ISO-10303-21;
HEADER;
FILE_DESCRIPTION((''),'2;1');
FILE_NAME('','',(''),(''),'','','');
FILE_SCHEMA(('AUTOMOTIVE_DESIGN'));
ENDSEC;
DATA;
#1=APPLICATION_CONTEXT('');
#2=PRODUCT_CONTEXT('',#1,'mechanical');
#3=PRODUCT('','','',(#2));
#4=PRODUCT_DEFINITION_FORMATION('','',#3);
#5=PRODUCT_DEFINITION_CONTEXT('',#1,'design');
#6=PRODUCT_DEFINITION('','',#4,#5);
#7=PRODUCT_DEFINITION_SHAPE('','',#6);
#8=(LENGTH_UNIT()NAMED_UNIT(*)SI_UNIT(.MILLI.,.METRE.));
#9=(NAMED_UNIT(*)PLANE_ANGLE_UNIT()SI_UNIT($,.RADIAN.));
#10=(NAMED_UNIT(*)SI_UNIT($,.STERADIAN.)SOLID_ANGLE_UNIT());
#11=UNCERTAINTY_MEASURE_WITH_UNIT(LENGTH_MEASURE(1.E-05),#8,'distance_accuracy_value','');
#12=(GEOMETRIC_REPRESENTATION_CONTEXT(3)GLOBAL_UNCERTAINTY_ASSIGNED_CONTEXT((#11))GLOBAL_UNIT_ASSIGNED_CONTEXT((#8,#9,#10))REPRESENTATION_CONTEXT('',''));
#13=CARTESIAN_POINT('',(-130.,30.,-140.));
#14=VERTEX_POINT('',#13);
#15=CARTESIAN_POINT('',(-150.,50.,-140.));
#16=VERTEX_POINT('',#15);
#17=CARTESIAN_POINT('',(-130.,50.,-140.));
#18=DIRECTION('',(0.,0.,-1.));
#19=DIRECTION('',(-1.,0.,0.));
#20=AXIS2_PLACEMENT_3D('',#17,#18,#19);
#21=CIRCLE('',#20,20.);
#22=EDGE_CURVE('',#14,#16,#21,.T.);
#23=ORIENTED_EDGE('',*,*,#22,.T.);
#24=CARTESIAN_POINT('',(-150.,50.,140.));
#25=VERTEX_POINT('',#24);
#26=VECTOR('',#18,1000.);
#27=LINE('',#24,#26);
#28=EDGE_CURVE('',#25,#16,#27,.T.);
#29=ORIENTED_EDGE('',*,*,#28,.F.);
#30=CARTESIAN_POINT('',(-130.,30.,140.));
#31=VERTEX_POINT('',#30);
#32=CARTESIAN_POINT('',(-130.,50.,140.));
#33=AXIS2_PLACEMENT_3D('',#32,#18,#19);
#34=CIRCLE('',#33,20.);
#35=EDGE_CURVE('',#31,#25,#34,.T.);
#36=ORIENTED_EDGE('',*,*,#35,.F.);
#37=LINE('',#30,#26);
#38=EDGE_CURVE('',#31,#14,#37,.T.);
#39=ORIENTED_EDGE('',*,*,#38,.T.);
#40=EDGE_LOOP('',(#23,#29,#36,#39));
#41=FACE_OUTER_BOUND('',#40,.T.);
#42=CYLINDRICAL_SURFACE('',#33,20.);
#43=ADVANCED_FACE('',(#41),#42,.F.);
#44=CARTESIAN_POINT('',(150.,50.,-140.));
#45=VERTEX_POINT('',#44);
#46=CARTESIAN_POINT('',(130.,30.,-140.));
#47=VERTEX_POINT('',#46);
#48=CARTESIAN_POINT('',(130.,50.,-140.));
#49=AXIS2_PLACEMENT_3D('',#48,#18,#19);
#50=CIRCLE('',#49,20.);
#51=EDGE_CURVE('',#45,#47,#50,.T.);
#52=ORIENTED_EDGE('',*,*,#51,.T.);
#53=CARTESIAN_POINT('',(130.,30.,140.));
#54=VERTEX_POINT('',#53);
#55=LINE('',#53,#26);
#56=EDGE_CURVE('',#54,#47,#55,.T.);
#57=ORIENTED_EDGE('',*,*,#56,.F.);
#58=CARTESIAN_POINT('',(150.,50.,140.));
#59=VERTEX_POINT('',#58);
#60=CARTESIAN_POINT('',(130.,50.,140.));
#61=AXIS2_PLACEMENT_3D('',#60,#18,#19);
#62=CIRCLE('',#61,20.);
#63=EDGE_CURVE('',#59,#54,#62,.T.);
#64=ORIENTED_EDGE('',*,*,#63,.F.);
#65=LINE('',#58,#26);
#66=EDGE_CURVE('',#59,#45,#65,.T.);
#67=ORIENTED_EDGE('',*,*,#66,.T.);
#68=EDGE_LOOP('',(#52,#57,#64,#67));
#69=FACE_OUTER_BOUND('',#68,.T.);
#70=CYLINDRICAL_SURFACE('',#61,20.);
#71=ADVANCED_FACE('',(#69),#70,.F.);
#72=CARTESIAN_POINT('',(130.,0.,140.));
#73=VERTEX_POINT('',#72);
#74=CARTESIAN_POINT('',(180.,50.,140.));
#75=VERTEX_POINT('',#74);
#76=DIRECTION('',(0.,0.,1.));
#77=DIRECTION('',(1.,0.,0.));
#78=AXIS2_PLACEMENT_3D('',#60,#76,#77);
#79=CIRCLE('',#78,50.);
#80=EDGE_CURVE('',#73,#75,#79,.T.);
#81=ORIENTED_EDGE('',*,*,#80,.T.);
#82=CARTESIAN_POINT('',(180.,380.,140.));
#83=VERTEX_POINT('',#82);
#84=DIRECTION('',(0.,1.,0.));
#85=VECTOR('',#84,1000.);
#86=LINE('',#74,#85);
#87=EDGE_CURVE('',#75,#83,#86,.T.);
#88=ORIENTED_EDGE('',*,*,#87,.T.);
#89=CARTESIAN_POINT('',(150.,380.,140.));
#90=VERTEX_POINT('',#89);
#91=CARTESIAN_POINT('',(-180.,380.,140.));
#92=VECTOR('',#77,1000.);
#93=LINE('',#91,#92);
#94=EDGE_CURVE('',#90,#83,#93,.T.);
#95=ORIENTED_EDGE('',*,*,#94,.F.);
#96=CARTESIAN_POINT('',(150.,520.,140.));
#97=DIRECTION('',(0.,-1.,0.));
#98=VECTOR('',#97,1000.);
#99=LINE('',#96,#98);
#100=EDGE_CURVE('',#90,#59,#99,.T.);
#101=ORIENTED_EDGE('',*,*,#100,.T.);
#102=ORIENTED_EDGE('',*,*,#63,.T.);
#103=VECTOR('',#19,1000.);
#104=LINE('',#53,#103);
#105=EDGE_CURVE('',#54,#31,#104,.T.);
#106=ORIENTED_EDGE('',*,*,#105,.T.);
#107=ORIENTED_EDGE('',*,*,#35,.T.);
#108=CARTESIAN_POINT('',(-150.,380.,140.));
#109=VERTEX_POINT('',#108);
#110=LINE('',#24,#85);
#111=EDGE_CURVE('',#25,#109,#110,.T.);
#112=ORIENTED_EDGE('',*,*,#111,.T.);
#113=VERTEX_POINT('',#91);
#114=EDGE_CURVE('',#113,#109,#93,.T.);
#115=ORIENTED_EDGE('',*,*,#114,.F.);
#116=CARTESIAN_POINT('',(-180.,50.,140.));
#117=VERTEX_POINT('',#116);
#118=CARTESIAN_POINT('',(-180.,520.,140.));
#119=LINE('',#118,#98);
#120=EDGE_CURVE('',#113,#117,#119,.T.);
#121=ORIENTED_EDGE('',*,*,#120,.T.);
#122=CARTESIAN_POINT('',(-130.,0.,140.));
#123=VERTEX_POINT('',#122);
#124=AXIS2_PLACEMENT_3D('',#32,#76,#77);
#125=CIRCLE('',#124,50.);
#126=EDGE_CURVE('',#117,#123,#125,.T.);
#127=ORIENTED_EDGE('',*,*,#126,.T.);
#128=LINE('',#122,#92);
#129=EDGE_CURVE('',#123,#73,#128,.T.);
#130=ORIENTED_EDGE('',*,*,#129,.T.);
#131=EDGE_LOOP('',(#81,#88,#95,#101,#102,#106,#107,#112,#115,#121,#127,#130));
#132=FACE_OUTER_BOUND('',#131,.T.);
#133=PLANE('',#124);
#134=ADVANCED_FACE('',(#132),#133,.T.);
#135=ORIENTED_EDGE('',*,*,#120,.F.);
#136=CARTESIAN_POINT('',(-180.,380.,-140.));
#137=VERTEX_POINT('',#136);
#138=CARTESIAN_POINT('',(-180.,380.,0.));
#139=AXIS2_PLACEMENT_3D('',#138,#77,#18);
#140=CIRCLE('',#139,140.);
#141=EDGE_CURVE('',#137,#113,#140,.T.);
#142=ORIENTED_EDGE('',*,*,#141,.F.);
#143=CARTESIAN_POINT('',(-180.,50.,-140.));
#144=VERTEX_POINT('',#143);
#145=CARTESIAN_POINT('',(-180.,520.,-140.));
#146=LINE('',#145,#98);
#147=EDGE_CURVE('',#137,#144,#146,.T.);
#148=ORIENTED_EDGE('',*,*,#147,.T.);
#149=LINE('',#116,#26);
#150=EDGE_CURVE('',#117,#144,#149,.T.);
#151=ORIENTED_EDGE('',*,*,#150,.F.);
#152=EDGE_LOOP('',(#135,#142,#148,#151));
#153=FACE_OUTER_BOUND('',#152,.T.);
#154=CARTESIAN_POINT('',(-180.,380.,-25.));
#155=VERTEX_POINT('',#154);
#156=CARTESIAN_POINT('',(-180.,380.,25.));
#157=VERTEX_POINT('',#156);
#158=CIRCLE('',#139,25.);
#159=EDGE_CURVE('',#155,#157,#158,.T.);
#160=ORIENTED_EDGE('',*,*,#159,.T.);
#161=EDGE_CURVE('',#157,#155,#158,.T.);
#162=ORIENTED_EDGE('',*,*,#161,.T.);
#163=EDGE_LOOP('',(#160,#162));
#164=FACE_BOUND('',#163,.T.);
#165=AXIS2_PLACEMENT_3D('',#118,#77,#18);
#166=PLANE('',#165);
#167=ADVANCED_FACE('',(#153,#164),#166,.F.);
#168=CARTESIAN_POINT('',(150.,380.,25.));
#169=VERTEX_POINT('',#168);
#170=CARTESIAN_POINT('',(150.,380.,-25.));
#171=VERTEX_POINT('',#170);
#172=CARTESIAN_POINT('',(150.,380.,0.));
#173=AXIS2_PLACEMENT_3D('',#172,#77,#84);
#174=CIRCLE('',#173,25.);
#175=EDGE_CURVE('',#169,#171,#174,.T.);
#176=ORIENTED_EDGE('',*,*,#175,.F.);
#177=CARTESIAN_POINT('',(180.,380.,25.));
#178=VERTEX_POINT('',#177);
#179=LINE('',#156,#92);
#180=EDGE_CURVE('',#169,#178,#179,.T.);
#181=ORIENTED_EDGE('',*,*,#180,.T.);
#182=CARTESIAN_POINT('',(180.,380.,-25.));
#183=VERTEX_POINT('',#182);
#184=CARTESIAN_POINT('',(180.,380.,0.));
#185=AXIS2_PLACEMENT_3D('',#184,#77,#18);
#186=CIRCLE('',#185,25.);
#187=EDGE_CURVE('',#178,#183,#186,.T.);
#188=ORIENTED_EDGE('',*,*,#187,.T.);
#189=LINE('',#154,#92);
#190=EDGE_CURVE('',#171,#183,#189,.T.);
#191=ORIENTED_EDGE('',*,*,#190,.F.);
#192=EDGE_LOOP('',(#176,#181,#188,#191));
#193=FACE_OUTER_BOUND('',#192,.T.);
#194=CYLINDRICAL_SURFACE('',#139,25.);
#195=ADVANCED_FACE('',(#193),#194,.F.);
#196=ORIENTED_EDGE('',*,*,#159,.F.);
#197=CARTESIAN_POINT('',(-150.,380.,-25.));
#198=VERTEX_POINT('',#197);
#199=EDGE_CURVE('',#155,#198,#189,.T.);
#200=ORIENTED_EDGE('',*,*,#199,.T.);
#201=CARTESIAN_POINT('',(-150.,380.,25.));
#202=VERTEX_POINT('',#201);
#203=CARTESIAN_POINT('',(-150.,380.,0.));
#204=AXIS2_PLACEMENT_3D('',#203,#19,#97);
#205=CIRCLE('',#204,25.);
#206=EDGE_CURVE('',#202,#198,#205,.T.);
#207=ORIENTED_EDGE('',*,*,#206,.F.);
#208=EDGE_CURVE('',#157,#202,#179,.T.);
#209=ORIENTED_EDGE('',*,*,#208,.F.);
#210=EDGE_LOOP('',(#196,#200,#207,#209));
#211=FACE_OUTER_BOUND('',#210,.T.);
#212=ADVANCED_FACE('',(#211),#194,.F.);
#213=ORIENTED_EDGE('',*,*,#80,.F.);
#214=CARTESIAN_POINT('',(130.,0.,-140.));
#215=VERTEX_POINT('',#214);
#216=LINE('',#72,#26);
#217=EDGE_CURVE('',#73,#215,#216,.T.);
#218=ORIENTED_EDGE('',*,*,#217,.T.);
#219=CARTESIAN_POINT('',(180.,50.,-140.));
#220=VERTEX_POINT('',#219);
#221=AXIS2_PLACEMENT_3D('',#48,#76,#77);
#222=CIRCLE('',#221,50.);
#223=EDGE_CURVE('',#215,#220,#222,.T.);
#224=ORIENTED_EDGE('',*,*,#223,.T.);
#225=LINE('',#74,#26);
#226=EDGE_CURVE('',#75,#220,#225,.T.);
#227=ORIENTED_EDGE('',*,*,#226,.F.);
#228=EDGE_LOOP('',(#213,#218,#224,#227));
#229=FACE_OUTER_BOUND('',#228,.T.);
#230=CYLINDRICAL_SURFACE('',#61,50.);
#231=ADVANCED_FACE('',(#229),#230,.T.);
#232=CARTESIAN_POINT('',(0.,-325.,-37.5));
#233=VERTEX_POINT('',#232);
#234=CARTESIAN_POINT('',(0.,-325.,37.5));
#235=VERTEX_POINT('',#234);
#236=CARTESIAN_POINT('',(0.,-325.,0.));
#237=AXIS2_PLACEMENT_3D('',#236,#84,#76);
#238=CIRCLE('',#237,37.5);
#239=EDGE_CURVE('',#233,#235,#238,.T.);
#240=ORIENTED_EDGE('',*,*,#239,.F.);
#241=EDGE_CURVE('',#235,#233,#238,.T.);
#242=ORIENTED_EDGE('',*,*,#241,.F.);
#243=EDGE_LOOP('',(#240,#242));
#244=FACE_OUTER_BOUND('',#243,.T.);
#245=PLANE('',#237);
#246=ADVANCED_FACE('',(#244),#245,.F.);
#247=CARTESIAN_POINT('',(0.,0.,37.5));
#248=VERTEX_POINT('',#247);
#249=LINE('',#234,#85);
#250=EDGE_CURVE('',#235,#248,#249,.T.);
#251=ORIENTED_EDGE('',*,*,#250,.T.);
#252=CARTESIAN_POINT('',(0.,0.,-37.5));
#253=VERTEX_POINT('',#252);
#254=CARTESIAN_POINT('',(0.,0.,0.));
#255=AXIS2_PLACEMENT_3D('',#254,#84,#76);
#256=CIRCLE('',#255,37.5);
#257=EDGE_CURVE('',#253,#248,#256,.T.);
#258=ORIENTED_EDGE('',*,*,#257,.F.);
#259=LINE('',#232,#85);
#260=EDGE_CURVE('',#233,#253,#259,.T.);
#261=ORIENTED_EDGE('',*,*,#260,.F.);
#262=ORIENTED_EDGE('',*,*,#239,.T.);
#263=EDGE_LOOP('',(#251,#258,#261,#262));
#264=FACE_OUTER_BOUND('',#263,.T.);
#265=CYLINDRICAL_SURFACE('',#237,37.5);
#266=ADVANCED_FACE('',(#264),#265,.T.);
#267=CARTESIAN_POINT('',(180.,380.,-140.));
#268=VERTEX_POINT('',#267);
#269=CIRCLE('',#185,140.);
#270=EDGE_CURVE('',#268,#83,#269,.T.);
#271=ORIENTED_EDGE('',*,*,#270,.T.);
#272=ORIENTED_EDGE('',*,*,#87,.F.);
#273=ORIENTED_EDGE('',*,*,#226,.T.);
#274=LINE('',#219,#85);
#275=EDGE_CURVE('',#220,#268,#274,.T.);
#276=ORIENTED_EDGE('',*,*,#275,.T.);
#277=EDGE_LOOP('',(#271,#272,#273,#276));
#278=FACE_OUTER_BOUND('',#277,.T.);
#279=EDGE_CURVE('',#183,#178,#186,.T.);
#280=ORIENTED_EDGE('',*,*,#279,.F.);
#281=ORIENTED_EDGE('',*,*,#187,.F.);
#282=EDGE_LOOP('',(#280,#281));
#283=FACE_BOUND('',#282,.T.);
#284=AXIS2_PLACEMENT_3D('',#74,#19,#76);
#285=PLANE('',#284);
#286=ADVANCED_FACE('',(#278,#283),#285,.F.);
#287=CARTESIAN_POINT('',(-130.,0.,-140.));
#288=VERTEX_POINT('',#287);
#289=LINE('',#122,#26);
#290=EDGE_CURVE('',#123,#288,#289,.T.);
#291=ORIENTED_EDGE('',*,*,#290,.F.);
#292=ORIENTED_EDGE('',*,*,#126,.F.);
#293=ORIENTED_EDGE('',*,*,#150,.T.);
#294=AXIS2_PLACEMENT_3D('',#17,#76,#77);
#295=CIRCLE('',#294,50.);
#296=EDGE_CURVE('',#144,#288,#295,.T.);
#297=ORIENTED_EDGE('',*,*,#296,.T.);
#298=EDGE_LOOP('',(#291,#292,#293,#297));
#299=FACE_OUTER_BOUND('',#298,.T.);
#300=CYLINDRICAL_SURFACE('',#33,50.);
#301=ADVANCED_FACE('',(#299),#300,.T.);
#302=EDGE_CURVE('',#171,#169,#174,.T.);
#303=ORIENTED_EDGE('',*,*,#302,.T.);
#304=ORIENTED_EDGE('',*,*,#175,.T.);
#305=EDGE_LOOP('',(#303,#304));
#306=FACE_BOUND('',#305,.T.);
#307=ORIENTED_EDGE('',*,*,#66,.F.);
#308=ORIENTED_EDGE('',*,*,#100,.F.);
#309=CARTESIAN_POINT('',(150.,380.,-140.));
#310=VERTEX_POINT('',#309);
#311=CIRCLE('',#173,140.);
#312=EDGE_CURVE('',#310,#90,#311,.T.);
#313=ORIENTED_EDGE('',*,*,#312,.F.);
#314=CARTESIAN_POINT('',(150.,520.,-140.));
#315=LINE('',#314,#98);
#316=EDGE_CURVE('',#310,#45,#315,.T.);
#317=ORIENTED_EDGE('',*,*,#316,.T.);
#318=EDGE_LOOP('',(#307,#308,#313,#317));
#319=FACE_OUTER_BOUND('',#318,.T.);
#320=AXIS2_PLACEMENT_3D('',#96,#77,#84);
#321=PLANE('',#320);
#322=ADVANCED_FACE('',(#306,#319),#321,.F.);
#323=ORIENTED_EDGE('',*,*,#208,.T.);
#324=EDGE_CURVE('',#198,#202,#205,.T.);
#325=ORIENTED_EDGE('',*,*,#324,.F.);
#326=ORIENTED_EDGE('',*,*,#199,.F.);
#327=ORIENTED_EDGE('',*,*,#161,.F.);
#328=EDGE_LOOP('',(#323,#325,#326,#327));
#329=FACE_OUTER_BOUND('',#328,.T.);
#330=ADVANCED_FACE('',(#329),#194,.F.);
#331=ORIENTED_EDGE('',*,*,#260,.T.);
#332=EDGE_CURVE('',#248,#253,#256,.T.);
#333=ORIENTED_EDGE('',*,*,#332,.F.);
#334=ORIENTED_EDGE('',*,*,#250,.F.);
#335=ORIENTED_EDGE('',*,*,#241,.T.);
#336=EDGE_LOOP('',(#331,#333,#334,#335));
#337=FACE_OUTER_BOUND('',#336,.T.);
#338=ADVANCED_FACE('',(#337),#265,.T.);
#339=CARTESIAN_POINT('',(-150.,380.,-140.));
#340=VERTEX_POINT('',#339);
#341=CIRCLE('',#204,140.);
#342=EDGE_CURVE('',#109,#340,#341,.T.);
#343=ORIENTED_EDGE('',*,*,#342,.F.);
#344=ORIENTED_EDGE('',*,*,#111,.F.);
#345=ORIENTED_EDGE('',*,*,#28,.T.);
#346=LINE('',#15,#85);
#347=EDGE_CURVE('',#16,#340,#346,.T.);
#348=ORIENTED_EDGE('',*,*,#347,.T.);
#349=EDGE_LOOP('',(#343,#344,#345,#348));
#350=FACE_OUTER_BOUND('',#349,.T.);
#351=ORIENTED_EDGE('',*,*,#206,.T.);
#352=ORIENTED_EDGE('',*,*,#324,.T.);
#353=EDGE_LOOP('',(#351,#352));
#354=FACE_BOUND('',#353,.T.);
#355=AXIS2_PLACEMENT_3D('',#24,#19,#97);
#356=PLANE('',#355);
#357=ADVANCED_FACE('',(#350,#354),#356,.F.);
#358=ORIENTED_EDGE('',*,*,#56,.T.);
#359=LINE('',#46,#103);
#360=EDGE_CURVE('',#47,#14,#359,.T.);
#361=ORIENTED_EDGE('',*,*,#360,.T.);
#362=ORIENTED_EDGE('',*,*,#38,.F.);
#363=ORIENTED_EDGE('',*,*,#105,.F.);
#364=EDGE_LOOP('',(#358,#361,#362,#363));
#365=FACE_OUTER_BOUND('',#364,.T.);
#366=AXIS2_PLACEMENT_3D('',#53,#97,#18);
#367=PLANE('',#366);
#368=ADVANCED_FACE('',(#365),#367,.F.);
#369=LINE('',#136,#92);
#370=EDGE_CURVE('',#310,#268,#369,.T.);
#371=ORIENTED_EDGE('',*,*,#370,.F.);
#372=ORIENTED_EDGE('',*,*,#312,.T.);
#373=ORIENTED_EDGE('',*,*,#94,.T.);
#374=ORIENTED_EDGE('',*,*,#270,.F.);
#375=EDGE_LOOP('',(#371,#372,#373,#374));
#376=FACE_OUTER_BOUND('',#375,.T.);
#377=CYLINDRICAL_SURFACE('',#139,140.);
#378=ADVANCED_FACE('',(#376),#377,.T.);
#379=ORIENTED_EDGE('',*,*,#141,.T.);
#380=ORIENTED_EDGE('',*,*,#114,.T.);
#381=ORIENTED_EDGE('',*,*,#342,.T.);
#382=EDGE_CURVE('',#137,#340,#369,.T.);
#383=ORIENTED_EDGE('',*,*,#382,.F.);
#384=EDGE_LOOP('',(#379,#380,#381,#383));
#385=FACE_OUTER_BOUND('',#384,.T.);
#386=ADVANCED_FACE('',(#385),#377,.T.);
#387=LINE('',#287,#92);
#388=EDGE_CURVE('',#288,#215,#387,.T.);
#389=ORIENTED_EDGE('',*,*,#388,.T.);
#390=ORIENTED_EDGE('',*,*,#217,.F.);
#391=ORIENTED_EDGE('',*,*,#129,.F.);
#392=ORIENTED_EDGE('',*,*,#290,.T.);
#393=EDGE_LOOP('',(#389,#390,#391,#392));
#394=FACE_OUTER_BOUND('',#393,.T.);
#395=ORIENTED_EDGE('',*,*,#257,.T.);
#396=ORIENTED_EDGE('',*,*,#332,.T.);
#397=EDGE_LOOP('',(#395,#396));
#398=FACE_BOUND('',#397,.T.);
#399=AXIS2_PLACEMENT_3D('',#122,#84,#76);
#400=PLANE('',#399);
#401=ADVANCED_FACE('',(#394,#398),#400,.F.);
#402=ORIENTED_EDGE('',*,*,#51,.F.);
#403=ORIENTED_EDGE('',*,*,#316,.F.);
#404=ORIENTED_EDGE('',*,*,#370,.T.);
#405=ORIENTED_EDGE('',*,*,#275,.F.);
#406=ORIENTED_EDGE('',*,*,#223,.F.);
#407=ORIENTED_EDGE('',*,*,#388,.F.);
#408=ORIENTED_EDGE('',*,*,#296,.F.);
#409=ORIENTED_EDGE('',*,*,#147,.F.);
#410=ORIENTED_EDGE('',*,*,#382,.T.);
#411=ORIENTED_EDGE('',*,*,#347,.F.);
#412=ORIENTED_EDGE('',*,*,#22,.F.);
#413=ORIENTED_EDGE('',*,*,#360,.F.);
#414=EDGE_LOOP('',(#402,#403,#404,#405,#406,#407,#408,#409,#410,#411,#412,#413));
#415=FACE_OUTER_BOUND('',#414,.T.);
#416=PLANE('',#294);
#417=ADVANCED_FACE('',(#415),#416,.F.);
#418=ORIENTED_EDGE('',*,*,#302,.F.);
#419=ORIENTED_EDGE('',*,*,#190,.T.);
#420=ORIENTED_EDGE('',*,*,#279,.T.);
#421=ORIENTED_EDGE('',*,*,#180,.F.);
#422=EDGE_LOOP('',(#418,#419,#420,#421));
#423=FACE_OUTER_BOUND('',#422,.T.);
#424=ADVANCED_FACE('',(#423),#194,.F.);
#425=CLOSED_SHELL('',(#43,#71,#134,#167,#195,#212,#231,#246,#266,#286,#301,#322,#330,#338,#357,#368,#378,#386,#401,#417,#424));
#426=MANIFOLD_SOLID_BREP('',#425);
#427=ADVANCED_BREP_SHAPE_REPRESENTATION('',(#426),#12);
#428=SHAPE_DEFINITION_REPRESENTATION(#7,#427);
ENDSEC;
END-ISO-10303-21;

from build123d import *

# Parameters (mm, degrees)
U_CHANNEL_BODY_DEPTH                  = 140
ROUNDED_ENDS_AND_PIN_HOLES_DEPTH      = 568.802782663
ROUNDED_ENDS_AND_PIN_HOLES_DEPTH_BACK = 568.802782663
ROUNDED_ENDS_AND_PIN_HOLE_SKETCH_R    = 25
SHANK_PROFILE_SKETCH_R                = 37.5
ROUND_SHANK_DEPTH                     = 355


with BuildPart() as part:
    # U-Channel Profile Sketch → U-Channel Body (new, symmetric)
    with BuildSketch(Plane.XY):
        with BuildLine():
            Line((-180, 520), (-180, 50))
            ThreePointArc((-180, 50), (-165.355339059, 14.644660941), (-130, 0))
            Line((-130, 0), (130, 0))
            ThreePointArc((130, 0), (165.355339059, 14.644660941), (180, 50))
            Line((180, 50), (180, 520))
            Line((180, 520), (150, 520))
            Line((150, 520), (150, 50))
            ThreePointArc((150, 50), (144.142135624, 35.857864376), (130, 30))
            Line((130, 30), (-130, 30))
            ThreePointArc((-130, 30), (-144.142135624, 35.857864376), (-150, 50))
            Line((-150, 50), (-150, 520))
            Line((-150, 520), (-180, 520))
        make_face()
    extrude(amount=U_CHANNEL_BODY_DEPTH, both=True)

    # Rounded Ends and Pin Hole Sketch → Rounded Ends and Pin Holes (cut, two sides: drawn at the far end of the back side and taken through both)
    with BuildSketch(Plane(origin=(0, 0, 0), x_dir=(0, 0, -1), z_dir=(1, 0, 0)).offset(-ROUNDED_ENDS_AND_PIN_HOLES_DEPTH_BACK)):
        with BuildLine():
            Line((-6.91e-07, 520), (-140, 520))
            Line((-140, 520), (-140, 380))
            ThreePointArc((-140, 380), (-98.99494961, 478.994949122), (-6.91e-07, 520))
        make_face()
        with BuildLine():
            Line((140, 520), (-6.91e-07, 520))
            ThreePointArc((-6.91e-07, 520), (98.994949122, 478.99494961), (140, 380))
            Line((140, 380), (140, 520))
        make_face()
        with Locations((0, 380)):
            Circle(ROUNDED_ENDS_AND_PIN_HOLE_SKETCH_R)
    extrude(amount=ROUNDED_ENDS_AND_PIN_HOLES_DEPTH + ROUNDED_ENDS_AND_PIN_HOLES_DEPTH_BACK, mode=Mode.SUBTRACT)

    # Shank Profile Sketch → Round Shank (add)
    with BuildSketch(Plane(origin=(0, 30, 0), x_dir=(1, 0, 0), z_dir=(0, 1, 0))):
        with Locations(Location((0, 0, 0), (0, 0, 270))):
            Circle(SHANK_PROFILE_SKETCH_R)
    extrude(amount=-ROUND_SHANK_DEPTH)


solid = part.part
